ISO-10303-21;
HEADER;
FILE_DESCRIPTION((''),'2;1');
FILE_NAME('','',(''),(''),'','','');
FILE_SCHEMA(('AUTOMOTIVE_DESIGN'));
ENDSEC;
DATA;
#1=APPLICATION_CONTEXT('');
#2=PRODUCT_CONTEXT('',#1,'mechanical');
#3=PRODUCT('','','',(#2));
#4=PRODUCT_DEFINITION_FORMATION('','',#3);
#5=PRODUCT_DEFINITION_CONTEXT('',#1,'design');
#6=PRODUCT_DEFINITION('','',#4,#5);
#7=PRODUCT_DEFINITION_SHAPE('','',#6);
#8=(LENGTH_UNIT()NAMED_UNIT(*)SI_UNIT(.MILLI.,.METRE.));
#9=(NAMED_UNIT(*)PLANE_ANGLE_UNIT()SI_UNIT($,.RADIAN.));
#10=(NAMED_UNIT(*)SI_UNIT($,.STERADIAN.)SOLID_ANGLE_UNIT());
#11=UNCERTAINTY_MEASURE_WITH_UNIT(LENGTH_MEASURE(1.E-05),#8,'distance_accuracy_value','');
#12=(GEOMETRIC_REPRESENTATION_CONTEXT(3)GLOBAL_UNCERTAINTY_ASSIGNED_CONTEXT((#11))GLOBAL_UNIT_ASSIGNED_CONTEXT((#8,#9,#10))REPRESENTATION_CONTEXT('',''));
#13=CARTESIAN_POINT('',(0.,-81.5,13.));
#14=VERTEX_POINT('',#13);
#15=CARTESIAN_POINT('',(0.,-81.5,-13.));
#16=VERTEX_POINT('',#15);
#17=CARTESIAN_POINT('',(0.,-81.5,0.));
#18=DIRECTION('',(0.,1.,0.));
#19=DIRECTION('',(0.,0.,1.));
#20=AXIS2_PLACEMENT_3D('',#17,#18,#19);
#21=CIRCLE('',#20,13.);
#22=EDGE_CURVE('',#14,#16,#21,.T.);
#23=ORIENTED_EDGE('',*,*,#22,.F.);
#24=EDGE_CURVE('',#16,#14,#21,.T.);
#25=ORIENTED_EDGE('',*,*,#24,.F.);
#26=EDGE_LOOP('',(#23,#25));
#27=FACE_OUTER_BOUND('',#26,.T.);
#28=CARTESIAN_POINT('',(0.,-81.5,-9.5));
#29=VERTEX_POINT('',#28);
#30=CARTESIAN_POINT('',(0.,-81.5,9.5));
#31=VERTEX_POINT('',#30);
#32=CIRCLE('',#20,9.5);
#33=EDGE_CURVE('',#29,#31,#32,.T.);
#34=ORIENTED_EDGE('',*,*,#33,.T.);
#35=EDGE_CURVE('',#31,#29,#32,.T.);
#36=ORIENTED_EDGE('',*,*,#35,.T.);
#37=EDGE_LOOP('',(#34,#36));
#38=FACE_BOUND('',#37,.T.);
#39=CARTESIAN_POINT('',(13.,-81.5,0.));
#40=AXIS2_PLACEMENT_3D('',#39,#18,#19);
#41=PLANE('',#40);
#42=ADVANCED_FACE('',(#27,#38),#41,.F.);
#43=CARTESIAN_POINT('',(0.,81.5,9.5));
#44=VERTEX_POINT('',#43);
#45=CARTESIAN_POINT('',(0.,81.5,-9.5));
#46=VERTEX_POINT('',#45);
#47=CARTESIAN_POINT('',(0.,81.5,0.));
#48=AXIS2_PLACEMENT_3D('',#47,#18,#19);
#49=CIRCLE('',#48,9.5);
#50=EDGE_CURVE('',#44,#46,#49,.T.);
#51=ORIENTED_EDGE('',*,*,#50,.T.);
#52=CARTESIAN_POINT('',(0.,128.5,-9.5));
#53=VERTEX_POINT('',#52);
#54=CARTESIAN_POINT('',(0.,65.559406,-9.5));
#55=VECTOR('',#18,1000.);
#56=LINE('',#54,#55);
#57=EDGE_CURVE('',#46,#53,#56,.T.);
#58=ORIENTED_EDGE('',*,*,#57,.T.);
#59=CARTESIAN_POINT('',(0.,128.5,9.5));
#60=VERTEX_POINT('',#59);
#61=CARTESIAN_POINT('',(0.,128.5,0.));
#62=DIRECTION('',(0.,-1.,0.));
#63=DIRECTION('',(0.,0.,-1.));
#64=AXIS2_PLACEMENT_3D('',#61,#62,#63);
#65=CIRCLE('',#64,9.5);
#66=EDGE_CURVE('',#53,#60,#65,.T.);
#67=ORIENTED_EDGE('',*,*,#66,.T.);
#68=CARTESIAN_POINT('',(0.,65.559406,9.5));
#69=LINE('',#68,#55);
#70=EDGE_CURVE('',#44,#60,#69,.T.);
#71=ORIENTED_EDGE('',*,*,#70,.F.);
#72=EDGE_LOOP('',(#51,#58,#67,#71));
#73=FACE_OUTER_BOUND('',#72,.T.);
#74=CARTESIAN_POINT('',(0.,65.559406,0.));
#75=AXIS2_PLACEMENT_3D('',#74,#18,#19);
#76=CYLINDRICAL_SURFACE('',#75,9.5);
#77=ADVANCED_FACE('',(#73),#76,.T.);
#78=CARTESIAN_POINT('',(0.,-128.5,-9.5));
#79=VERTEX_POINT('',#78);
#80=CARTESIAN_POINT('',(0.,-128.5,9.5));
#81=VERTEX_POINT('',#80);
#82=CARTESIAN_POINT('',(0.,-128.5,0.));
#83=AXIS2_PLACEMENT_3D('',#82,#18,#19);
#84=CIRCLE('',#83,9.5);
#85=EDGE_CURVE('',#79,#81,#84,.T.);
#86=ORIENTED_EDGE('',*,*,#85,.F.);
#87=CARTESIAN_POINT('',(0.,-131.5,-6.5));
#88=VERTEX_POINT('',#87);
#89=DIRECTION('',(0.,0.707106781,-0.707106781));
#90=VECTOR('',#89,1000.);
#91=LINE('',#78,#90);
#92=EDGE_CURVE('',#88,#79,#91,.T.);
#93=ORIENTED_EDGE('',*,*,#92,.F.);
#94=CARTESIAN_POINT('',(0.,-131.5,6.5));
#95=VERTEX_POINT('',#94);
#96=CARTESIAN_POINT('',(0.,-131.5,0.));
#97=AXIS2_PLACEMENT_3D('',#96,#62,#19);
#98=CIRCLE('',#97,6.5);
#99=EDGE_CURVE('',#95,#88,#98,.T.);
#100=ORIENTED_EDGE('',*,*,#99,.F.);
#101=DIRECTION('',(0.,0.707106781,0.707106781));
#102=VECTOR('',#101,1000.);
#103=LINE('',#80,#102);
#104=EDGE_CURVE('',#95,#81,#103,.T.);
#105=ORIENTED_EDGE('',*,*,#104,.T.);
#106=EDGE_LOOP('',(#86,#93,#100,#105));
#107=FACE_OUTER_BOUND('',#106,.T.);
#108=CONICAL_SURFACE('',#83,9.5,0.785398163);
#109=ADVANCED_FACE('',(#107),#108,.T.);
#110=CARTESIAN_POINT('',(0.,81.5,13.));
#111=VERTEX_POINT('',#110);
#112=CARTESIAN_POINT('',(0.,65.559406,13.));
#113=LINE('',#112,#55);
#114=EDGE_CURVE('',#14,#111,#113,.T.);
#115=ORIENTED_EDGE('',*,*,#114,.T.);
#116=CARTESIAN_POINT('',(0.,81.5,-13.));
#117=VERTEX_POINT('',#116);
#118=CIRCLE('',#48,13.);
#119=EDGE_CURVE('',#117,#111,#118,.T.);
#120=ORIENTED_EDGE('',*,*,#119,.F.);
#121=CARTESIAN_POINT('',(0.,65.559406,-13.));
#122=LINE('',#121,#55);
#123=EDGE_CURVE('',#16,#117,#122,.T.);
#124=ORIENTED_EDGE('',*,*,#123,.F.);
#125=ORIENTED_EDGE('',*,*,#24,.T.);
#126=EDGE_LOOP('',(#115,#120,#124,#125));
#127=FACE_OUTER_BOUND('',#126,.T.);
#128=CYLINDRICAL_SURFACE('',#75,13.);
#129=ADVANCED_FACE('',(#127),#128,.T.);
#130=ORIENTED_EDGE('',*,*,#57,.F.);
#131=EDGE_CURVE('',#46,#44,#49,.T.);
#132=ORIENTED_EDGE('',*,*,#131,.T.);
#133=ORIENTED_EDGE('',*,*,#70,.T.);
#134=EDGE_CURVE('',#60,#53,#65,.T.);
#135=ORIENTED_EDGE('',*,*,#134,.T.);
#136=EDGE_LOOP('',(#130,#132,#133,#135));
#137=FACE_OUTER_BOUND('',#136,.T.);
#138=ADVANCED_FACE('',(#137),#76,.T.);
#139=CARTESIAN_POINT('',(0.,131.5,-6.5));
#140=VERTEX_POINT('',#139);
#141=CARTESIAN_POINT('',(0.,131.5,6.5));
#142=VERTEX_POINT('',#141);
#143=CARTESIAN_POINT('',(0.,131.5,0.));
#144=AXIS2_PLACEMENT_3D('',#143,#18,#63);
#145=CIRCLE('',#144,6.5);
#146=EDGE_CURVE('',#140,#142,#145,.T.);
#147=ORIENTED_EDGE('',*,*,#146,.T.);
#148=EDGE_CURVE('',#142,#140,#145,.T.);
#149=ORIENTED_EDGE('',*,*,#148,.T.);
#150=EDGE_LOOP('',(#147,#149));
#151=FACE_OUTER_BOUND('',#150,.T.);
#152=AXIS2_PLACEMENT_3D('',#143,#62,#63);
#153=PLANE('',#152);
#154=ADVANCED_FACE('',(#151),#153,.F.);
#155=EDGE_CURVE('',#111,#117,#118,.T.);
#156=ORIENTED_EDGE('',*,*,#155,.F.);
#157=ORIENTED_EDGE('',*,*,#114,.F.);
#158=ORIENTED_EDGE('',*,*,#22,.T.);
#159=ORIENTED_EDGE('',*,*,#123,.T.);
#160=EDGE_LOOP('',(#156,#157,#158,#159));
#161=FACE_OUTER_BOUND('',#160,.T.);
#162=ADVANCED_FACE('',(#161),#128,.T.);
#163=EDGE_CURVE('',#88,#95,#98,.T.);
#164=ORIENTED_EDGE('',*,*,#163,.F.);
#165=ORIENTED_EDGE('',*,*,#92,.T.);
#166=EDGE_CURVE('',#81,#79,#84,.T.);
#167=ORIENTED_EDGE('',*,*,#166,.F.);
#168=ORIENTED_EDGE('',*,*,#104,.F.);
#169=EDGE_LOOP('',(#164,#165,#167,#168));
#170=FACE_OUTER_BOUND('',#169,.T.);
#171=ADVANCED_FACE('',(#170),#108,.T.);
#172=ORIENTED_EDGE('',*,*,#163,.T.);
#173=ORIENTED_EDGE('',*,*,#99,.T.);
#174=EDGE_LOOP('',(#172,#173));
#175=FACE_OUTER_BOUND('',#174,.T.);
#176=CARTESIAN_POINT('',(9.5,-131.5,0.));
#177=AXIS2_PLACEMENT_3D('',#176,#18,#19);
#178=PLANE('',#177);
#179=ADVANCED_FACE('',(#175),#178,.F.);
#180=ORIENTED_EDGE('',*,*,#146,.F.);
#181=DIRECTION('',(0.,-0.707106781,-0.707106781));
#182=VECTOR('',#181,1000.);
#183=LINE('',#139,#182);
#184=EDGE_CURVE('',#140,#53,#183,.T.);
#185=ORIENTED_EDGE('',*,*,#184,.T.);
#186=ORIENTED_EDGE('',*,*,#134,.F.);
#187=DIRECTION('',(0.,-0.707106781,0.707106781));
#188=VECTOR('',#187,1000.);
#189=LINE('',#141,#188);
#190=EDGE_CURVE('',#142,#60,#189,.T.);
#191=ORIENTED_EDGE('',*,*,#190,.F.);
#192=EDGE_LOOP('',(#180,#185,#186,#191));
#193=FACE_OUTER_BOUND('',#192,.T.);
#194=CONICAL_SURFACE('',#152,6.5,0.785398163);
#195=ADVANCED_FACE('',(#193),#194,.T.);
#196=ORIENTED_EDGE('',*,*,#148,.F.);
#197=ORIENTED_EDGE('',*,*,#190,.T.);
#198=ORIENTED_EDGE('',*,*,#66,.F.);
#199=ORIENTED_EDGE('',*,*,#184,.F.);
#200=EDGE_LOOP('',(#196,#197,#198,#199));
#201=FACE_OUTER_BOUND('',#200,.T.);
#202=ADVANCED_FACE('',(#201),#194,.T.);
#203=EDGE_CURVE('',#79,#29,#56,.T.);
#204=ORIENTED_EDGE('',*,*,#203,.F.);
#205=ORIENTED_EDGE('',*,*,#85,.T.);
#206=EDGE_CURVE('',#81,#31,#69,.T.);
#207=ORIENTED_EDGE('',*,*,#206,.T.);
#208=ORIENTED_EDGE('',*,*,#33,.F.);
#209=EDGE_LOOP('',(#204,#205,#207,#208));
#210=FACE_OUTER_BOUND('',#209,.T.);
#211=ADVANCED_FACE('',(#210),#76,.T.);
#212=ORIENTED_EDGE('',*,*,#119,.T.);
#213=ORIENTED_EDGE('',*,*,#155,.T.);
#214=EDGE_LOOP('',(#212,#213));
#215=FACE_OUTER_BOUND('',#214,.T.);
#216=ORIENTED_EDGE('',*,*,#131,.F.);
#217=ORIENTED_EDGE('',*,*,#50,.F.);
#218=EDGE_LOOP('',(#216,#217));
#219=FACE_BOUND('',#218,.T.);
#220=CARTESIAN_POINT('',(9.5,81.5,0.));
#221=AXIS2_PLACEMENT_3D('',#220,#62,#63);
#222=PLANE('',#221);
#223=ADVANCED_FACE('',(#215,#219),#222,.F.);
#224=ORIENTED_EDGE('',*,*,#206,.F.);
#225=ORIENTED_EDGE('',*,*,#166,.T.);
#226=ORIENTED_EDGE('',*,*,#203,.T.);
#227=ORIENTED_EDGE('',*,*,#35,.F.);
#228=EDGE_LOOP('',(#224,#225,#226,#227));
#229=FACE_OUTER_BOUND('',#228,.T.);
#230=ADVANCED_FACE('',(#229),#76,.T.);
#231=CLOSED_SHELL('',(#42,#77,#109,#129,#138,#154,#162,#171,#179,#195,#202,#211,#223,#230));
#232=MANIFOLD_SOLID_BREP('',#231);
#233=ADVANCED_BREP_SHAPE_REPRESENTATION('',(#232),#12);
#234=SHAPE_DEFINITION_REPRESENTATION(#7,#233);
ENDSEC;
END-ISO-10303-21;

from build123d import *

# Parameters (mm, degrees)
END_CHAMFERS_3X45_SIZE = 3


with BuildPart() as part:
    # Pin Profile Sketch → Pin Body Revolve (revolve)
    with BuildSketch(Plane.XY, mode=Mode.PRIVATE) as pin_body_revolve_sk:
        Polygon((0, 131.5), (9.5, 131.5), (9.5, 81.5), (13, 81.5), (13, -81.5), (9.5, -81.5), (9.5, -131.5), (0, -131.5), align=None)
    revolve(pin_body_revolve_sk.sketch.rotate(Axis((0, 65.559405941, 0), (0, -1, 0)), 90), axis=Axis((0, 65.559405941, 0), (0, -1, 0)))

    # End Chamfers 3x45°
    end_chamfers_3x45_edges = [part.edges().sort_by_distance(p)[0] for p in [
        (0, -131.5, -9.5),
        (0, 131.5, -9.5),
    ]]
    chamfer(end_chamfers_3x45_edges, length=END_CHAMFERS_3X45_SIZE)


solid = part.part
